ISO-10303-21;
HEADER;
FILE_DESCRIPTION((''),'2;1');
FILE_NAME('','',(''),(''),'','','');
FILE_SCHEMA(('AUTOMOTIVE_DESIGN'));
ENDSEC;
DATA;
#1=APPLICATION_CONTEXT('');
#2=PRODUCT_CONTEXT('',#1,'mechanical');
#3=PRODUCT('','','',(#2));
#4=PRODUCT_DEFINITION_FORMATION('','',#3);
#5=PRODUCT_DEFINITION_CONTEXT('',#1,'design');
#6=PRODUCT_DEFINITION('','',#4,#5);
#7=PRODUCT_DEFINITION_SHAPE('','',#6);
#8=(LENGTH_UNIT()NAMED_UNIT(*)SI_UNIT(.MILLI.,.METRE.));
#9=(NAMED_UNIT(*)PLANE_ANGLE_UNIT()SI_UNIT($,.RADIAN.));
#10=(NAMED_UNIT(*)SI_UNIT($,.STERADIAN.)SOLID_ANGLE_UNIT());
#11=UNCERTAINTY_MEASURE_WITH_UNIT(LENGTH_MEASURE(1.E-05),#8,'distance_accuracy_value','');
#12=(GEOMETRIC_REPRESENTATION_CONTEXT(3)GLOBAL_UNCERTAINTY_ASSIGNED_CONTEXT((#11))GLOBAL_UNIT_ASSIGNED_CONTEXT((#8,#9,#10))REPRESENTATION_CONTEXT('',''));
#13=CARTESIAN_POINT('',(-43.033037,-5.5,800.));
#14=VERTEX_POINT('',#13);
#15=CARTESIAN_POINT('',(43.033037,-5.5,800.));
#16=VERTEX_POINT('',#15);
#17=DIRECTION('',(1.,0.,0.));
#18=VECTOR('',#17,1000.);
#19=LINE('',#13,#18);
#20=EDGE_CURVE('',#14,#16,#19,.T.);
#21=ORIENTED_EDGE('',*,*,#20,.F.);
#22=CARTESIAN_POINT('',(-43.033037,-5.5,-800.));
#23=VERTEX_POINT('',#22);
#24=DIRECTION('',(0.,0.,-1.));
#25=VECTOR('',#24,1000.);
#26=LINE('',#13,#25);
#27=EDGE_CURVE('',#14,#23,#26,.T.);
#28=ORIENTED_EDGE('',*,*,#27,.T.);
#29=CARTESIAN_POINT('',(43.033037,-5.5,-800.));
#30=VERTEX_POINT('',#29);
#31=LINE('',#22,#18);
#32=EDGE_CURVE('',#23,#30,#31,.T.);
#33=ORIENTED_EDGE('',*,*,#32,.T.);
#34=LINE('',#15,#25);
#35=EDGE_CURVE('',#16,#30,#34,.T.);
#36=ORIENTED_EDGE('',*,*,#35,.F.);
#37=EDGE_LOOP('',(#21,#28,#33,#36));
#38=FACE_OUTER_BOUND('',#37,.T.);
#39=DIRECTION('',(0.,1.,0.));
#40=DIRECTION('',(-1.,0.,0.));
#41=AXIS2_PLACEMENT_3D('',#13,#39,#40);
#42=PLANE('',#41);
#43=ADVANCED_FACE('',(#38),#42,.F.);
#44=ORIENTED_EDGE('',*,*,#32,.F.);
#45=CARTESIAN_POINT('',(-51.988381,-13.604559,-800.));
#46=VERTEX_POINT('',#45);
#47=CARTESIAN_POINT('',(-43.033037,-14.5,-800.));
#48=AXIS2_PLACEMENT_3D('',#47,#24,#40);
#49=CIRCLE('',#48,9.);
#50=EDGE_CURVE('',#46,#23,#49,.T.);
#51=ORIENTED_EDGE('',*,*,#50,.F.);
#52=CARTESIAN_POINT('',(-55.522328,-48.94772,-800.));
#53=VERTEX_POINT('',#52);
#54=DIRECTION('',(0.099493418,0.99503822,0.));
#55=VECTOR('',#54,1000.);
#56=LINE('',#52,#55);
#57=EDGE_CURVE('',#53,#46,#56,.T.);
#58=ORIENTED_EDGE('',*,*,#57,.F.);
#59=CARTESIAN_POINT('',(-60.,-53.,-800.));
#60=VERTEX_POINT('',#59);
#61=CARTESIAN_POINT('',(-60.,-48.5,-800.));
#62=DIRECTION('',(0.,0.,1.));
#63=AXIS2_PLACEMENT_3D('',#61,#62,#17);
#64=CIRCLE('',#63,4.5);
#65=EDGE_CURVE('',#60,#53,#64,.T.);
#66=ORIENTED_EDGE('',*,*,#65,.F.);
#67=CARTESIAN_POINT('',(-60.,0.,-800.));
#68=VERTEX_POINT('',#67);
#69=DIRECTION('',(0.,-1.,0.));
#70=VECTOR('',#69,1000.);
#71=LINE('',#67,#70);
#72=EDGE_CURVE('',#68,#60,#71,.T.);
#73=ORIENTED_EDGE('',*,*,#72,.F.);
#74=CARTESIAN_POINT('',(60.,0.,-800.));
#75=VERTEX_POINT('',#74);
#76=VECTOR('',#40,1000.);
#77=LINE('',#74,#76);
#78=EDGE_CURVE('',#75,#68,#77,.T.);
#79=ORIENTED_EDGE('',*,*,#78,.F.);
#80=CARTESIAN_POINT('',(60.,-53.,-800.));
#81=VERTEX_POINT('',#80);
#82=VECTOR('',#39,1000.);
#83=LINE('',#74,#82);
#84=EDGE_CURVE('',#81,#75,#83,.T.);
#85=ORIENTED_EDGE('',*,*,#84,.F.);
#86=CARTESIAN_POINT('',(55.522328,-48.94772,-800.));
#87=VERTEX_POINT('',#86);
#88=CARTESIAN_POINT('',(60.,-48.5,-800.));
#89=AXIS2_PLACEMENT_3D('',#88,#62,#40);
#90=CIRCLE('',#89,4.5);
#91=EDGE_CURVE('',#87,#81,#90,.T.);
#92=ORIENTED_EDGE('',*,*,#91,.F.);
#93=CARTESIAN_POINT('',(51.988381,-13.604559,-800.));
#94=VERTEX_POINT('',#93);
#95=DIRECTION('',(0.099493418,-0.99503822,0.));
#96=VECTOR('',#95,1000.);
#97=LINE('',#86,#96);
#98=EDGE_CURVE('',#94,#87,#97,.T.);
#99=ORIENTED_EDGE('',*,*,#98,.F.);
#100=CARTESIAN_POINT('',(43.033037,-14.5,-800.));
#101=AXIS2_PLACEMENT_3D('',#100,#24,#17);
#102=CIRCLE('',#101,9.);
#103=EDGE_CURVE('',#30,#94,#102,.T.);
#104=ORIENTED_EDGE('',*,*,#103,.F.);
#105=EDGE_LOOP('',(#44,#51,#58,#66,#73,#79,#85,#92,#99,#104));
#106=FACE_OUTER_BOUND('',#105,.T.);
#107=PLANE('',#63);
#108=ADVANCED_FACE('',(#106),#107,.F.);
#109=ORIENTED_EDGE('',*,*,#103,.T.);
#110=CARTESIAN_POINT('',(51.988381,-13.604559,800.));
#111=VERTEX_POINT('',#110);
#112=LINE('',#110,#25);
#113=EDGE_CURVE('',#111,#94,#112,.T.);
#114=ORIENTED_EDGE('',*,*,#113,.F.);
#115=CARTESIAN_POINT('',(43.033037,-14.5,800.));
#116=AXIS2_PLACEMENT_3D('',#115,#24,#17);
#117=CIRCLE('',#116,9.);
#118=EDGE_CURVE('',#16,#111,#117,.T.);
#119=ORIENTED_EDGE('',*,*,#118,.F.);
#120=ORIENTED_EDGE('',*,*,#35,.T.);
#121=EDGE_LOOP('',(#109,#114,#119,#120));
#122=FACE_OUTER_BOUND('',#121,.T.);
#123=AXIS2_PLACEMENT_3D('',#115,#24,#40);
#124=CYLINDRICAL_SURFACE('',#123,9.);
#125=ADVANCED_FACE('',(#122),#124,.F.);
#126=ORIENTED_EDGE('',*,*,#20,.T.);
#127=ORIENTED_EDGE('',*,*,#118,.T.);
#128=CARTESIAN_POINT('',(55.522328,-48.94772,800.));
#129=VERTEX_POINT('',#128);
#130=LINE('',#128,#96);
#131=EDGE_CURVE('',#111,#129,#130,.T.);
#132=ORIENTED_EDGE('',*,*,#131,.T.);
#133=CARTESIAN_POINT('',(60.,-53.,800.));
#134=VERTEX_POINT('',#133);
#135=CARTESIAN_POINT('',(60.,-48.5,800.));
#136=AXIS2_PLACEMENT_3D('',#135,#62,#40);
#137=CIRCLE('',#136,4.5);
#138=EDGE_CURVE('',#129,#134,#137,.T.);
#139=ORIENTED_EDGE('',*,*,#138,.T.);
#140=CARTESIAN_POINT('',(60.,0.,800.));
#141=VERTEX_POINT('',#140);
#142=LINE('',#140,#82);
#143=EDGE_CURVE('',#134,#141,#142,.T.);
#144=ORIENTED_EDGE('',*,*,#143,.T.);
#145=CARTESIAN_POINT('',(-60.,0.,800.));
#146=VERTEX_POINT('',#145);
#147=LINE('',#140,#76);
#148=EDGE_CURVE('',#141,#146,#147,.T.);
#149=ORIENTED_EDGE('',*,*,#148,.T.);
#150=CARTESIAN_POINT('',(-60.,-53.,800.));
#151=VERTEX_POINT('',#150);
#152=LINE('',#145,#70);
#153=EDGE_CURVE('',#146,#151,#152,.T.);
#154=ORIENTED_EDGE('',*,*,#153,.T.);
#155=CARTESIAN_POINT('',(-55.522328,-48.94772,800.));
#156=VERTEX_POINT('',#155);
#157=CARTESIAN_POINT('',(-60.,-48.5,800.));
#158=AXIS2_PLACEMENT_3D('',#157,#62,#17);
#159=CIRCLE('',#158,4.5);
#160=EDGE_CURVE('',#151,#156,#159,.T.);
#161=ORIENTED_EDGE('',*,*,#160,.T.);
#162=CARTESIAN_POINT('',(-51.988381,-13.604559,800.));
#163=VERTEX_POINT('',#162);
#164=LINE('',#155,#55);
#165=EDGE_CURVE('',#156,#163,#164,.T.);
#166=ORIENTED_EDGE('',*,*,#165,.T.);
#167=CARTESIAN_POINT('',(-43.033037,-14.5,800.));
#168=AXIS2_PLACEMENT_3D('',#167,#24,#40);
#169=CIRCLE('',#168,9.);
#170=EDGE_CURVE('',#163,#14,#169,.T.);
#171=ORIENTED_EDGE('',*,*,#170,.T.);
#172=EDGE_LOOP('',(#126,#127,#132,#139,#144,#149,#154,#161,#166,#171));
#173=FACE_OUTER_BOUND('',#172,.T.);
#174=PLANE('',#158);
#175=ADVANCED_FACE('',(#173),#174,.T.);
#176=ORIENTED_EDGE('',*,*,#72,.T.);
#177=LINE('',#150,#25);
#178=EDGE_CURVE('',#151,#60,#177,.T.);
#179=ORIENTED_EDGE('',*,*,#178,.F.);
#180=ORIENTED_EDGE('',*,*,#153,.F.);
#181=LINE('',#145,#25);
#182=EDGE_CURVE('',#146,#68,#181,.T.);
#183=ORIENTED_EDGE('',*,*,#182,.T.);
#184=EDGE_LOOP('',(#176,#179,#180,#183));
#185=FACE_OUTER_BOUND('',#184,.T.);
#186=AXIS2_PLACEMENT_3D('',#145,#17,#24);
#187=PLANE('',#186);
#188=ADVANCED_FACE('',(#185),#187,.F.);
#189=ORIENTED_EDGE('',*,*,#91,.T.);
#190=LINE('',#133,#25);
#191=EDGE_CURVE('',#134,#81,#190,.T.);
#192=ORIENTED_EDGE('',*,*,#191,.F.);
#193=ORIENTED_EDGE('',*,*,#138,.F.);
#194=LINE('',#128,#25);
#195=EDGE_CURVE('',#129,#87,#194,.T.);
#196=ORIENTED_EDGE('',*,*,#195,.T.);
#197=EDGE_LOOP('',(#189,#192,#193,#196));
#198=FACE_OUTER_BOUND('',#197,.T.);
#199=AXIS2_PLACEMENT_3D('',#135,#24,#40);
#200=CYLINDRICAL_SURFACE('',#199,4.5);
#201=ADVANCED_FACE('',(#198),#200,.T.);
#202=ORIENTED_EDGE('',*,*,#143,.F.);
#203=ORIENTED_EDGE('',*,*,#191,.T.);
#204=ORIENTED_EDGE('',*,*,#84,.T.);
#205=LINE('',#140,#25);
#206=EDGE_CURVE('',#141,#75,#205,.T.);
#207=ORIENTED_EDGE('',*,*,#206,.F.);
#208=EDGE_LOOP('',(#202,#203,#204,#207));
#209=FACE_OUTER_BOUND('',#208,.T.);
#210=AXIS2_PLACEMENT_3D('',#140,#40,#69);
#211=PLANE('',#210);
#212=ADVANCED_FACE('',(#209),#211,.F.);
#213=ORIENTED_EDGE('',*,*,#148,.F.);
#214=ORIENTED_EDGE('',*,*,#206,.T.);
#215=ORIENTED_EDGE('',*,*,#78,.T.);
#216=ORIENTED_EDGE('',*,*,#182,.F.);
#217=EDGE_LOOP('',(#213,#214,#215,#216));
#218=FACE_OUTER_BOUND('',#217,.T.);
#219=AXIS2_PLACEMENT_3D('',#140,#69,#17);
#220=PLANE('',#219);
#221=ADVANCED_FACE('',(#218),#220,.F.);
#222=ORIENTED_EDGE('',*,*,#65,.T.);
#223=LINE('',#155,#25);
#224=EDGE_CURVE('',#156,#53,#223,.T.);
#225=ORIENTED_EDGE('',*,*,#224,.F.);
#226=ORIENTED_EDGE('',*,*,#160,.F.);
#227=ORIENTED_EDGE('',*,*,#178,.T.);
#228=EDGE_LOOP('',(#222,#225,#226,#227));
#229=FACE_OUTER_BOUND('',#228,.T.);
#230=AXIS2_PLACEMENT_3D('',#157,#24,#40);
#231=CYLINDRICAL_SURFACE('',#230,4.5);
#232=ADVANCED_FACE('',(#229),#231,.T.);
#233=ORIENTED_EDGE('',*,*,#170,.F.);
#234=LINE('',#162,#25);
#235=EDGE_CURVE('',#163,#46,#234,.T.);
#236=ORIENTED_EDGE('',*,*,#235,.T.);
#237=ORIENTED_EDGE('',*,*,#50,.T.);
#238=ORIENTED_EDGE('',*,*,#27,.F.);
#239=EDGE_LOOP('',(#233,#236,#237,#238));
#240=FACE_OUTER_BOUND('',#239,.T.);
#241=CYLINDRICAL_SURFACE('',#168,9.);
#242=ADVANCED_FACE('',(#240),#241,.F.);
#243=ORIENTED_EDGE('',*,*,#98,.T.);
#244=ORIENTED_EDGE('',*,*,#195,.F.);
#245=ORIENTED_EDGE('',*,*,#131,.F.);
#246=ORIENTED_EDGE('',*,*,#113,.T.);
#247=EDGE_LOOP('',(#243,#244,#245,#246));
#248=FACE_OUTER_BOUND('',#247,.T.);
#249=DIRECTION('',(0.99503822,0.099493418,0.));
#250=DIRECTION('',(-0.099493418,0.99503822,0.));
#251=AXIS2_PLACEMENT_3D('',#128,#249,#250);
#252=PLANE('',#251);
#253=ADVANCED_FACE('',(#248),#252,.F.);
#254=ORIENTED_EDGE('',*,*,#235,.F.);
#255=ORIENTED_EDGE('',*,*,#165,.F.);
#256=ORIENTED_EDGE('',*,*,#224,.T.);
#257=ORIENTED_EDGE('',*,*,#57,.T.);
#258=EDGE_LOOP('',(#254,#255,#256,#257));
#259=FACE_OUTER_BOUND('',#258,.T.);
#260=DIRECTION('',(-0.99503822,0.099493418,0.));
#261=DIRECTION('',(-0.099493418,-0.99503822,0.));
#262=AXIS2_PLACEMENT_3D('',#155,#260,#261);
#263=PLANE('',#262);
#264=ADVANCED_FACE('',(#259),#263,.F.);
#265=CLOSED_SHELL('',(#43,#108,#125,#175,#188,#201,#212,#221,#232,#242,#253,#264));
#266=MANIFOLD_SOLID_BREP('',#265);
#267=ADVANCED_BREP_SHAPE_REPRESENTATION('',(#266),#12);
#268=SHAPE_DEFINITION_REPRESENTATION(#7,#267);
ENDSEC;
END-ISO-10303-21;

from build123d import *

# Parameters (mm, degrees)
BOSS_EXTRUDE_1_DEPTH = 800


with BuildPart() as part:
    # Sketch 1 → Boss-Extrude 1 (new, symmetric)
    with BuildSketch(Plane.XY):
        with BuildLine():
            Line((60, 0), (-60, 0))
            Line((-60, 0), (-60, -53))
            ThreePointArc((-60, -53), (-56.980458786, -51.836520772), (-55.522328009, -48.947720382))
            Line((-55.522328009, -48.947720382), (-51.988381432, -13.604559236))
            ThreePointArc((-51.988381432, -13.604559236), (-49.072119877, -7.826958457), (-43.03303745, -5.5))
            Line((-43.03303745, -5.5), (43.03303745, -5.5))
            ThreePointArc((43.03303745, -5.5), (49.072119877, -7.826958457), (51.988381432, -13.604559236))
            Line((51.988381432, -13.604559236), (55.522328009, -48.947720382))
            ThreePointArc((55.522328009, -48.947720382), (56.980458786, -51.836520772), (60, -53))
            Line((60, -53), (60, 0))
        make_face()
    extrude(amount=BOSS_EXTRUDE_1_DEPTH, both=True)


solid = part.part
